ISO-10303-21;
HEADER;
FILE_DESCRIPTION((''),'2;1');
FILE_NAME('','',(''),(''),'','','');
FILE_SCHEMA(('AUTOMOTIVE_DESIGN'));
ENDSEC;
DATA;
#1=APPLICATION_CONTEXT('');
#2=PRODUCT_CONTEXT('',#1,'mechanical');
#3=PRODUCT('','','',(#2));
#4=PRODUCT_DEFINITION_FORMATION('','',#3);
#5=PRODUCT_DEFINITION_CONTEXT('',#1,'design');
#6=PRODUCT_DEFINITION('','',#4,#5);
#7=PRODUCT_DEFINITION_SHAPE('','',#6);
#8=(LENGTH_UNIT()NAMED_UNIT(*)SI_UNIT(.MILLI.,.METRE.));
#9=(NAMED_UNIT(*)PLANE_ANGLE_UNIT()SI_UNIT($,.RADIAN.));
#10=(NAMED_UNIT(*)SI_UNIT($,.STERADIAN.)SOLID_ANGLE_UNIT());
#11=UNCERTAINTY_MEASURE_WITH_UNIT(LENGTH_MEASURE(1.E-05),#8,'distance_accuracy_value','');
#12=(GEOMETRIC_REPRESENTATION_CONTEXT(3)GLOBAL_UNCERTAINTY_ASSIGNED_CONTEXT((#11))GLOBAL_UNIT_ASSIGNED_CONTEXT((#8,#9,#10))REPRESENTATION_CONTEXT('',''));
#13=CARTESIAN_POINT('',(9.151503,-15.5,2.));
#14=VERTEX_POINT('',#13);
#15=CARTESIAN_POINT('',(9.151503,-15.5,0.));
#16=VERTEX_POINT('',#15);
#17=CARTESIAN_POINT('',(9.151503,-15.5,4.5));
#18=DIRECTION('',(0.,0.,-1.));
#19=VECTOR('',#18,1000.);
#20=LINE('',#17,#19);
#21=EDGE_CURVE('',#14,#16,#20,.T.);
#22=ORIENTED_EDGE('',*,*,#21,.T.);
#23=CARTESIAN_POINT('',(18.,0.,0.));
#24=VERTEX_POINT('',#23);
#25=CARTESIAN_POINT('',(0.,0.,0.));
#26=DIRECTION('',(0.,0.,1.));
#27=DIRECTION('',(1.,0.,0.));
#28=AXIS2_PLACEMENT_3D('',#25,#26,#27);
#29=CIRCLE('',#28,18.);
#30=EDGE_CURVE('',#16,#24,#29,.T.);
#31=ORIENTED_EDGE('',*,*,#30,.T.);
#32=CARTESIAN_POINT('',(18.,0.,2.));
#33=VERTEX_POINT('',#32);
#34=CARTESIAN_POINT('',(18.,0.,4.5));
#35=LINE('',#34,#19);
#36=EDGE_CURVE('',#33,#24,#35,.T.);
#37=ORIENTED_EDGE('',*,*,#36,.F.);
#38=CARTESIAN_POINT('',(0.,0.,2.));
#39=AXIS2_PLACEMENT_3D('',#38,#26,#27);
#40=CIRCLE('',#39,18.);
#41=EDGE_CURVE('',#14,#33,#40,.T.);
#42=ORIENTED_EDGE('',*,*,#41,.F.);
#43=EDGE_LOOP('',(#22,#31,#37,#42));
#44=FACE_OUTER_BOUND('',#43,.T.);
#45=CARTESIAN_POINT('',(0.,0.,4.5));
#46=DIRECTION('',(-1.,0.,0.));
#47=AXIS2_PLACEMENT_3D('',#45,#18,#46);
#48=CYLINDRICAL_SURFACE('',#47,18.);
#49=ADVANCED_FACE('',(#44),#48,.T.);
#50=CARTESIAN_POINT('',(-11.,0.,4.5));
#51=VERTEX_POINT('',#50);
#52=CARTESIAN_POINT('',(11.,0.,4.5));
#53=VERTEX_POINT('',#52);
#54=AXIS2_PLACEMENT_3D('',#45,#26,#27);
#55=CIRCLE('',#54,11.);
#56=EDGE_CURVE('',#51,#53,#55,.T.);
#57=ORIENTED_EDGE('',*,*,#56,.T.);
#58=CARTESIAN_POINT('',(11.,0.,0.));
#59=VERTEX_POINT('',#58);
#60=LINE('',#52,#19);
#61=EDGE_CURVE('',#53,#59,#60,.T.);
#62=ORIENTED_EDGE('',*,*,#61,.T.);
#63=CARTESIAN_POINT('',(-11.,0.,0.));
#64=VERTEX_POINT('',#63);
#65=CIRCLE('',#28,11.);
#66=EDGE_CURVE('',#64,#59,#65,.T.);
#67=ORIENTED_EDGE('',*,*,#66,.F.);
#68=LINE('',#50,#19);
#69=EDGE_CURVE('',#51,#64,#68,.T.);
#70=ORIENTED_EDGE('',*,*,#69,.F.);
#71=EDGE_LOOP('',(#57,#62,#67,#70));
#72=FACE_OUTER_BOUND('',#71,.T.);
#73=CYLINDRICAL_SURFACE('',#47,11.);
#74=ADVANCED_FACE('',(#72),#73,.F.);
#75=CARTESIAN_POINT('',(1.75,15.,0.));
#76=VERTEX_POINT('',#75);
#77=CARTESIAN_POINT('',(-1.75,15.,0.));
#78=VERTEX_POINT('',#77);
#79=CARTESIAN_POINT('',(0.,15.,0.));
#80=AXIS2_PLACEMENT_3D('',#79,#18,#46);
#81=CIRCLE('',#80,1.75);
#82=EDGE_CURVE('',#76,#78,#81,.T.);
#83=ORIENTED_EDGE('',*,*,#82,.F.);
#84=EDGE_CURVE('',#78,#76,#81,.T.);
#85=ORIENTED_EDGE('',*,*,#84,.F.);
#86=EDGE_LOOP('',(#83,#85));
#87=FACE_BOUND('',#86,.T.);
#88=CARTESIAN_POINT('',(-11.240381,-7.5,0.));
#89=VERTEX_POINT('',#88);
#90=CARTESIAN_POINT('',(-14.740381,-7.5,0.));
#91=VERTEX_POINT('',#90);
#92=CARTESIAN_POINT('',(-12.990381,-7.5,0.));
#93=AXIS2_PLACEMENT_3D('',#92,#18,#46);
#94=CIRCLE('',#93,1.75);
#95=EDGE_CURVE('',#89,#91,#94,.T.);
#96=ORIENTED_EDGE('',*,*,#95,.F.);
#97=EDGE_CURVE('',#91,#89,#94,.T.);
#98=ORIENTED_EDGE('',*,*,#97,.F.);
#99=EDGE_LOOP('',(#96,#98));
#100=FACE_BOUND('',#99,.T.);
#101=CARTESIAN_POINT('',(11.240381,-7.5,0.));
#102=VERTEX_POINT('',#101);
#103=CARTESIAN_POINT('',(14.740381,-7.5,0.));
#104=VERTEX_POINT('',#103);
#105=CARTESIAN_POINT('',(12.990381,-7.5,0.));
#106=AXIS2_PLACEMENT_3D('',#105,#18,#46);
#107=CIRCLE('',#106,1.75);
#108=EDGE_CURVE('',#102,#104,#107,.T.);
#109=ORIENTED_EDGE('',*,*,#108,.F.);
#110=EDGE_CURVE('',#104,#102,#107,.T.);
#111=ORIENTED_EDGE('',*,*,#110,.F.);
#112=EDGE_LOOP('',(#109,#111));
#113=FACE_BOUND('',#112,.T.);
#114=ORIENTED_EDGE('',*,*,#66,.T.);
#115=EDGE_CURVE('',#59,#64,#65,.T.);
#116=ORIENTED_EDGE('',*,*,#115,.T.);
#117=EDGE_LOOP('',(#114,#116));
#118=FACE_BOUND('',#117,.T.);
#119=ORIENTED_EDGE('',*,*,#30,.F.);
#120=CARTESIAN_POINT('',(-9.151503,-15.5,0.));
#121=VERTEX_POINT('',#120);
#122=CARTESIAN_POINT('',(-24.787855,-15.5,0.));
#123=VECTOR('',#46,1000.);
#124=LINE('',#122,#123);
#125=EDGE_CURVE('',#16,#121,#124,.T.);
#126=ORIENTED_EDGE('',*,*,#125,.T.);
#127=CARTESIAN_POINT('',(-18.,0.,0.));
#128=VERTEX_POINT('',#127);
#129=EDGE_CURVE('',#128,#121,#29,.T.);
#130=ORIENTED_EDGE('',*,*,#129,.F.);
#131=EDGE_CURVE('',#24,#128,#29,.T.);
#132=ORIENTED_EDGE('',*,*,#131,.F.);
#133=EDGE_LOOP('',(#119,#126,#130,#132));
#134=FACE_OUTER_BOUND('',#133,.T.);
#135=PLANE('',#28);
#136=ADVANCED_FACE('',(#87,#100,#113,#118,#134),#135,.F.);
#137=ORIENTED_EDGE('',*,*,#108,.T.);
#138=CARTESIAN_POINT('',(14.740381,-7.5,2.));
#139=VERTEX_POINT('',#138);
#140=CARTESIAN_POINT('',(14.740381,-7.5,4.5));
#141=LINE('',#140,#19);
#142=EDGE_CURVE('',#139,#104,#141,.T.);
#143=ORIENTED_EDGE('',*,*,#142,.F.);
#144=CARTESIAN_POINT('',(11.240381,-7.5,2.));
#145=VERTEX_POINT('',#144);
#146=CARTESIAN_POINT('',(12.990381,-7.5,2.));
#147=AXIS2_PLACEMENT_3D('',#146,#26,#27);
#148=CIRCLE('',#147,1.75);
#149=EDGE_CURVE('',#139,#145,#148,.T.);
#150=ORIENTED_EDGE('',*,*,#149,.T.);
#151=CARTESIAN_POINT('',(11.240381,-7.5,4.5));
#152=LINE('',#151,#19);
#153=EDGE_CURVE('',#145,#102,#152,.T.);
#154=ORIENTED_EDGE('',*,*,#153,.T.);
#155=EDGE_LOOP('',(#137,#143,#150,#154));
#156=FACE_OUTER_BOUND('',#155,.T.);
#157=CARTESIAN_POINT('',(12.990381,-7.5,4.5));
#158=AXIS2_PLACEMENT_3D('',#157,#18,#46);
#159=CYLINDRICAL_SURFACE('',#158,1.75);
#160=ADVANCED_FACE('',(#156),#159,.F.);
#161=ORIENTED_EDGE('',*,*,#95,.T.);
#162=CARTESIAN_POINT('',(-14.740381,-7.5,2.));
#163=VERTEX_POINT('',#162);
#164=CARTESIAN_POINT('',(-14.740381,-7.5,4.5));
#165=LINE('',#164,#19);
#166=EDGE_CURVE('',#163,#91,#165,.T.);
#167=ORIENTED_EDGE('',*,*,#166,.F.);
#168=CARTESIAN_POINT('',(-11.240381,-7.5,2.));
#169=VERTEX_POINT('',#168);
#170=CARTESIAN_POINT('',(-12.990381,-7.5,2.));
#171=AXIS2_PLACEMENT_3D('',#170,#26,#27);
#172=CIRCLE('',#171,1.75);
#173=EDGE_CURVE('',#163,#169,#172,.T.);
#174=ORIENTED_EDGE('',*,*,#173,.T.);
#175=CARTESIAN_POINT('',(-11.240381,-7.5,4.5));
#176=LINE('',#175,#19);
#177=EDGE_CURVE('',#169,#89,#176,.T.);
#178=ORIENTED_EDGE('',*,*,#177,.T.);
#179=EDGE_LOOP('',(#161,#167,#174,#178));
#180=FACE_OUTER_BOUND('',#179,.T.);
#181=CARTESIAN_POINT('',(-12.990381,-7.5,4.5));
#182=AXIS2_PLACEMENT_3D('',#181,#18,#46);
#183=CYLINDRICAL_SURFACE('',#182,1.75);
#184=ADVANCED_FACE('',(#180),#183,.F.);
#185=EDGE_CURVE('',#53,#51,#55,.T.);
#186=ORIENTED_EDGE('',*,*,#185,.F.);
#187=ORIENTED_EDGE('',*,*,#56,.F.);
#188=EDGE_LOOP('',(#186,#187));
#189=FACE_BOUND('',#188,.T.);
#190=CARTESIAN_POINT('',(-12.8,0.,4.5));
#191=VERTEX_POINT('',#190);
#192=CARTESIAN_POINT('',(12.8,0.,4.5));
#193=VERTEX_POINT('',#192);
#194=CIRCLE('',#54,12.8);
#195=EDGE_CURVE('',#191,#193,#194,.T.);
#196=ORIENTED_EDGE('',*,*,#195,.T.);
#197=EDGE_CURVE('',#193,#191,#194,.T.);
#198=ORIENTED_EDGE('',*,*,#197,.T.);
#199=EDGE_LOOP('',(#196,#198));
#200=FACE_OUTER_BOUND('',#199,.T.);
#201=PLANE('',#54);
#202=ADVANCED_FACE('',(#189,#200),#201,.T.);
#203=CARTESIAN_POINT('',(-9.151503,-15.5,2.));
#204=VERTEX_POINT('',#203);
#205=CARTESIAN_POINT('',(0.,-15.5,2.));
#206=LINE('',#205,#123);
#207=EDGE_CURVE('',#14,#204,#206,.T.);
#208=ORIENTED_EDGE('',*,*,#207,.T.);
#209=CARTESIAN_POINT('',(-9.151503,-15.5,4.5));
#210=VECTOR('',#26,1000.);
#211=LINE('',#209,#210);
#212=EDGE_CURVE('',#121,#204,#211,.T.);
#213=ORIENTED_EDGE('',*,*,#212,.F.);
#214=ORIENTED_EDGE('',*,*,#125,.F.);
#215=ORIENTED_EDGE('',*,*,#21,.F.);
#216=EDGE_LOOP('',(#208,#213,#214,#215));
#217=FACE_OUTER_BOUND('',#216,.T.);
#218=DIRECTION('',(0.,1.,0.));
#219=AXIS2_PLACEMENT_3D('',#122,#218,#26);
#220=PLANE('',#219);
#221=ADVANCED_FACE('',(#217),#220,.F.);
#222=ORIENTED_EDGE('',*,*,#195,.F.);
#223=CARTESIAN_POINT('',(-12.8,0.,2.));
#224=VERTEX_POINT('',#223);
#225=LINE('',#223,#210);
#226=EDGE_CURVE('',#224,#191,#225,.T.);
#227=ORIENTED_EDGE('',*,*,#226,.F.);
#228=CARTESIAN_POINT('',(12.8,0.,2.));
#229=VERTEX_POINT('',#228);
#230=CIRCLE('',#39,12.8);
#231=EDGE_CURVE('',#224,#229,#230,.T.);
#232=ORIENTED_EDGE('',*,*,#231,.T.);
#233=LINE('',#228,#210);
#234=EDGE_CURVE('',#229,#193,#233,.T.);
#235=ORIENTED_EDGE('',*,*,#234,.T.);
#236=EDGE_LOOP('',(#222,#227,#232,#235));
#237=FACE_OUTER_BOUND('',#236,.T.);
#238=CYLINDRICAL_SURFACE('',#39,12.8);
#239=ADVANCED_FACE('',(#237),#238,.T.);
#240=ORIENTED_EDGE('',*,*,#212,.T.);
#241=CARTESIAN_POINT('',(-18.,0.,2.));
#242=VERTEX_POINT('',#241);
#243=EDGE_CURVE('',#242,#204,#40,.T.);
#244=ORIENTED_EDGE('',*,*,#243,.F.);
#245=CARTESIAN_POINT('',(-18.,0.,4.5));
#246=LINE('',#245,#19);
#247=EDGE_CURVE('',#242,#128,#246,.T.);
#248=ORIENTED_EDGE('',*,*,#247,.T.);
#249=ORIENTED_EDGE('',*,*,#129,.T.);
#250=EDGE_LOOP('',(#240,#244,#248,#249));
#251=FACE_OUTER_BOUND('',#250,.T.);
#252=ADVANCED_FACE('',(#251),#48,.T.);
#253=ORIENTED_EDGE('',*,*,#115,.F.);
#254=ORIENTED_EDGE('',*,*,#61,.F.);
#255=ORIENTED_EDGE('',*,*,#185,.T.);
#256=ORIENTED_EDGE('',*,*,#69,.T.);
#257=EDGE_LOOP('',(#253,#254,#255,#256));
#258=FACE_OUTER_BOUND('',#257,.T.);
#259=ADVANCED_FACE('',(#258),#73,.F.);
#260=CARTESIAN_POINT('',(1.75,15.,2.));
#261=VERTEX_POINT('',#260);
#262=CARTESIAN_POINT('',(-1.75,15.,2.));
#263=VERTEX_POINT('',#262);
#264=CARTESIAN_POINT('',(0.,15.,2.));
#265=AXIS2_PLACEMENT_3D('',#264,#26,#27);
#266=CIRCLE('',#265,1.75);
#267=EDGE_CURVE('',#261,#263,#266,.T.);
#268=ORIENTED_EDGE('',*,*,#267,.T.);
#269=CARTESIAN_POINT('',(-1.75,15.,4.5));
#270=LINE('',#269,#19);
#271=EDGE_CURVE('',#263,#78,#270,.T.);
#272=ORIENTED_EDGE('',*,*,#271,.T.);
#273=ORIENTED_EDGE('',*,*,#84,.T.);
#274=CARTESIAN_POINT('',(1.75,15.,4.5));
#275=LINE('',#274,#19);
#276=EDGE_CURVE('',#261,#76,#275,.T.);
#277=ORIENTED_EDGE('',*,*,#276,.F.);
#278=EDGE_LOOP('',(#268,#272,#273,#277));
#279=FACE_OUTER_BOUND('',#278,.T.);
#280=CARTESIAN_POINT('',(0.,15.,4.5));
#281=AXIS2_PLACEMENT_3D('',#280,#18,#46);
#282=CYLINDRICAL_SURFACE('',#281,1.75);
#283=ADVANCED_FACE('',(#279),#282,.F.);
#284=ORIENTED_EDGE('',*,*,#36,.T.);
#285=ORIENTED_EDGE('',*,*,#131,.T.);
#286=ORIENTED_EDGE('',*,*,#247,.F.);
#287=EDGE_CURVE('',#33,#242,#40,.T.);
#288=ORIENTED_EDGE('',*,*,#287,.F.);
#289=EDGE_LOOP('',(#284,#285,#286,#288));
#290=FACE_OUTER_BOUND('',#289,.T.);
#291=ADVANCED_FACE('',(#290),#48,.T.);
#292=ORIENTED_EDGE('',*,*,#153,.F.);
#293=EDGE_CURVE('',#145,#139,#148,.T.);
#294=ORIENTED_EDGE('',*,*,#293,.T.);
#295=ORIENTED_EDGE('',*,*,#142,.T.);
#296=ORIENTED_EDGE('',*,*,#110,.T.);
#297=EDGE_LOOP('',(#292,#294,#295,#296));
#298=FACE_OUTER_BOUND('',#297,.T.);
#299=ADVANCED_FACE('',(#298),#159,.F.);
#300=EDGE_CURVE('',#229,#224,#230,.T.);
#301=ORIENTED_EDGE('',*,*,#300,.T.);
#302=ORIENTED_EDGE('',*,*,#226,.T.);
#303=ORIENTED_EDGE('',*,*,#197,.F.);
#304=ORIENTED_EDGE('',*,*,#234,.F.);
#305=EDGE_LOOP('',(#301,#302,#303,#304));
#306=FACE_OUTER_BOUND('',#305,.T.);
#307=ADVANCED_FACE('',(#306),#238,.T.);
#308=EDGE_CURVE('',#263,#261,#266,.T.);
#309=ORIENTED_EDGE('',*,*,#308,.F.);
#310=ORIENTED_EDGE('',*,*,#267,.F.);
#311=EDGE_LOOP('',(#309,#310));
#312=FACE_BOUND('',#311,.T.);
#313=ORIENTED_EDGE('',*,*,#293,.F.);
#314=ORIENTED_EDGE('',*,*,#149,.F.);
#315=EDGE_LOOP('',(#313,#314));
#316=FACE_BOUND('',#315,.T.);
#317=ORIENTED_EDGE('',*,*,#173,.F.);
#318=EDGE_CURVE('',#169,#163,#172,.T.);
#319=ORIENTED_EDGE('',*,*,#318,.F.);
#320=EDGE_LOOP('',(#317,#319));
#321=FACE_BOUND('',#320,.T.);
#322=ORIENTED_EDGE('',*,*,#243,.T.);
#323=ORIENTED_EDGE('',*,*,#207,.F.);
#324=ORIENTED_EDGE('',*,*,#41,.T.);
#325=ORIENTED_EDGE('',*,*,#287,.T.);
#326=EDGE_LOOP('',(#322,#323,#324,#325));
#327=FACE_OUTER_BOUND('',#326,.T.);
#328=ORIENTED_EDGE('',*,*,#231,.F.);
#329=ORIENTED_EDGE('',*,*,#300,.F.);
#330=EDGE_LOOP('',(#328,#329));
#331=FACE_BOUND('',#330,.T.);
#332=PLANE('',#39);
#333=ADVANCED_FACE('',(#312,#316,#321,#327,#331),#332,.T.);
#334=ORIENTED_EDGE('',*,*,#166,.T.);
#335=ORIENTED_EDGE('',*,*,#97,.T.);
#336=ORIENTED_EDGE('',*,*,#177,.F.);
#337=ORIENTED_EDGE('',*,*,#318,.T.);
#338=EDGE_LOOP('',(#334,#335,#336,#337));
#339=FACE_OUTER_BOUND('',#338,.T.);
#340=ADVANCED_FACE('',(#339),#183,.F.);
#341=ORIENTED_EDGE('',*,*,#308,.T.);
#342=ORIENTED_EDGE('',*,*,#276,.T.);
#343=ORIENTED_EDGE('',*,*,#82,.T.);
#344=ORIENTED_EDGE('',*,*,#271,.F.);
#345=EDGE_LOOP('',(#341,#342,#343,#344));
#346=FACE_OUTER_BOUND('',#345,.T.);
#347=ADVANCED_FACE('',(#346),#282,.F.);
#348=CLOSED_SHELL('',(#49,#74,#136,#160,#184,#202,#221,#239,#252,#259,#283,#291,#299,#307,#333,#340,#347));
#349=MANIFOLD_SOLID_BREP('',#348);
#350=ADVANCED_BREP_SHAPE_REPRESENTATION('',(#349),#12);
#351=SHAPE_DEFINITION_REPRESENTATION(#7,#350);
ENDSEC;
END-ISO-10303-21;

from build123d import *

# Parameters (mm, degrees)
SKETCH_1_R          = 18
SKETCH_1_R_2        = 11
EXTRUDE_1_DEPTH     = 4.5
SKETCH_2_OUTSIDE_W  = 48.222
SKETCH_2_OUTSIDE_H  = 48.222
SKETCH_2_OUTSIDE_R  = 12.8
CUT_EXTRUDE_1_DEPTH = 2.5
SKETCH_3_W          = 45.784626658
SKETCH_3_H          = 5.372844692
CUT_EXTRUDE_2_DEPTH = 26.578311125
SKETCH_4_R          = 1.75
CUT_EXTRUDE_3_DEPTH = 26.850531909


with BuildPart() as part:
    # 草图1 → 凸台-拉伸1 (new body)
    with BuildSketch(Plane.XY):
        Circle(SKETCH_1_R)
        Circle(SKETCH_1_R_2, mode=Mode.SUBTRACT)
    extrude(amount=EXTRUDE_1_DEPTH)

    # 草图2 outside → 切除-拉伸1 (cut)
    with BuildSketch(Plane.XY.offset(4.5)):
        Rectangle(SKETCH_2_OUTSIDE_W, SKETCH_2_OUTSIDE_H)
        Circle(SKETCH_2_OUTSIDE_R, mode=Mode.SUBTRACT)
    extrude(amount=-CUT_EXTRUDE_1_DEPTH, mode=Mode.SUBTRACT)

    # 草图3 → 切除-拉伸2 (cut, through all)
    with BuildSketch(Plane.XY.offset(2)):
        with Locations((-1.895541868, -18.186422346)):
            Rectangle(SKETCH_3_W, SKETCH_3_H)
    extrude(amount=-CUT_EXTRUDE_2_DEPTH, mode=Mode.SUBTRACT)

    # 草图4 → 切除-拉伸3 (cut, through all)
    with BuildSketch(Plane(origin=(0, 0, 0), x_dir=(-1, 0, 0), z_dir=(0, 0, -1))):
        with Locations((0, 15)):
            Circle(SKETCH_4_R)
        with Locations((-12.990381057, -7.5)):
            Circle(SKETCH_4_R)
        with Locations((12.990381057, -7.5)):
            Circle(SKETCH_4_R)
    extrude(amount=-CUT_EXTRUDE_3_DEPTH, mode=Mode.SUBTRACT)


solid = part.part
